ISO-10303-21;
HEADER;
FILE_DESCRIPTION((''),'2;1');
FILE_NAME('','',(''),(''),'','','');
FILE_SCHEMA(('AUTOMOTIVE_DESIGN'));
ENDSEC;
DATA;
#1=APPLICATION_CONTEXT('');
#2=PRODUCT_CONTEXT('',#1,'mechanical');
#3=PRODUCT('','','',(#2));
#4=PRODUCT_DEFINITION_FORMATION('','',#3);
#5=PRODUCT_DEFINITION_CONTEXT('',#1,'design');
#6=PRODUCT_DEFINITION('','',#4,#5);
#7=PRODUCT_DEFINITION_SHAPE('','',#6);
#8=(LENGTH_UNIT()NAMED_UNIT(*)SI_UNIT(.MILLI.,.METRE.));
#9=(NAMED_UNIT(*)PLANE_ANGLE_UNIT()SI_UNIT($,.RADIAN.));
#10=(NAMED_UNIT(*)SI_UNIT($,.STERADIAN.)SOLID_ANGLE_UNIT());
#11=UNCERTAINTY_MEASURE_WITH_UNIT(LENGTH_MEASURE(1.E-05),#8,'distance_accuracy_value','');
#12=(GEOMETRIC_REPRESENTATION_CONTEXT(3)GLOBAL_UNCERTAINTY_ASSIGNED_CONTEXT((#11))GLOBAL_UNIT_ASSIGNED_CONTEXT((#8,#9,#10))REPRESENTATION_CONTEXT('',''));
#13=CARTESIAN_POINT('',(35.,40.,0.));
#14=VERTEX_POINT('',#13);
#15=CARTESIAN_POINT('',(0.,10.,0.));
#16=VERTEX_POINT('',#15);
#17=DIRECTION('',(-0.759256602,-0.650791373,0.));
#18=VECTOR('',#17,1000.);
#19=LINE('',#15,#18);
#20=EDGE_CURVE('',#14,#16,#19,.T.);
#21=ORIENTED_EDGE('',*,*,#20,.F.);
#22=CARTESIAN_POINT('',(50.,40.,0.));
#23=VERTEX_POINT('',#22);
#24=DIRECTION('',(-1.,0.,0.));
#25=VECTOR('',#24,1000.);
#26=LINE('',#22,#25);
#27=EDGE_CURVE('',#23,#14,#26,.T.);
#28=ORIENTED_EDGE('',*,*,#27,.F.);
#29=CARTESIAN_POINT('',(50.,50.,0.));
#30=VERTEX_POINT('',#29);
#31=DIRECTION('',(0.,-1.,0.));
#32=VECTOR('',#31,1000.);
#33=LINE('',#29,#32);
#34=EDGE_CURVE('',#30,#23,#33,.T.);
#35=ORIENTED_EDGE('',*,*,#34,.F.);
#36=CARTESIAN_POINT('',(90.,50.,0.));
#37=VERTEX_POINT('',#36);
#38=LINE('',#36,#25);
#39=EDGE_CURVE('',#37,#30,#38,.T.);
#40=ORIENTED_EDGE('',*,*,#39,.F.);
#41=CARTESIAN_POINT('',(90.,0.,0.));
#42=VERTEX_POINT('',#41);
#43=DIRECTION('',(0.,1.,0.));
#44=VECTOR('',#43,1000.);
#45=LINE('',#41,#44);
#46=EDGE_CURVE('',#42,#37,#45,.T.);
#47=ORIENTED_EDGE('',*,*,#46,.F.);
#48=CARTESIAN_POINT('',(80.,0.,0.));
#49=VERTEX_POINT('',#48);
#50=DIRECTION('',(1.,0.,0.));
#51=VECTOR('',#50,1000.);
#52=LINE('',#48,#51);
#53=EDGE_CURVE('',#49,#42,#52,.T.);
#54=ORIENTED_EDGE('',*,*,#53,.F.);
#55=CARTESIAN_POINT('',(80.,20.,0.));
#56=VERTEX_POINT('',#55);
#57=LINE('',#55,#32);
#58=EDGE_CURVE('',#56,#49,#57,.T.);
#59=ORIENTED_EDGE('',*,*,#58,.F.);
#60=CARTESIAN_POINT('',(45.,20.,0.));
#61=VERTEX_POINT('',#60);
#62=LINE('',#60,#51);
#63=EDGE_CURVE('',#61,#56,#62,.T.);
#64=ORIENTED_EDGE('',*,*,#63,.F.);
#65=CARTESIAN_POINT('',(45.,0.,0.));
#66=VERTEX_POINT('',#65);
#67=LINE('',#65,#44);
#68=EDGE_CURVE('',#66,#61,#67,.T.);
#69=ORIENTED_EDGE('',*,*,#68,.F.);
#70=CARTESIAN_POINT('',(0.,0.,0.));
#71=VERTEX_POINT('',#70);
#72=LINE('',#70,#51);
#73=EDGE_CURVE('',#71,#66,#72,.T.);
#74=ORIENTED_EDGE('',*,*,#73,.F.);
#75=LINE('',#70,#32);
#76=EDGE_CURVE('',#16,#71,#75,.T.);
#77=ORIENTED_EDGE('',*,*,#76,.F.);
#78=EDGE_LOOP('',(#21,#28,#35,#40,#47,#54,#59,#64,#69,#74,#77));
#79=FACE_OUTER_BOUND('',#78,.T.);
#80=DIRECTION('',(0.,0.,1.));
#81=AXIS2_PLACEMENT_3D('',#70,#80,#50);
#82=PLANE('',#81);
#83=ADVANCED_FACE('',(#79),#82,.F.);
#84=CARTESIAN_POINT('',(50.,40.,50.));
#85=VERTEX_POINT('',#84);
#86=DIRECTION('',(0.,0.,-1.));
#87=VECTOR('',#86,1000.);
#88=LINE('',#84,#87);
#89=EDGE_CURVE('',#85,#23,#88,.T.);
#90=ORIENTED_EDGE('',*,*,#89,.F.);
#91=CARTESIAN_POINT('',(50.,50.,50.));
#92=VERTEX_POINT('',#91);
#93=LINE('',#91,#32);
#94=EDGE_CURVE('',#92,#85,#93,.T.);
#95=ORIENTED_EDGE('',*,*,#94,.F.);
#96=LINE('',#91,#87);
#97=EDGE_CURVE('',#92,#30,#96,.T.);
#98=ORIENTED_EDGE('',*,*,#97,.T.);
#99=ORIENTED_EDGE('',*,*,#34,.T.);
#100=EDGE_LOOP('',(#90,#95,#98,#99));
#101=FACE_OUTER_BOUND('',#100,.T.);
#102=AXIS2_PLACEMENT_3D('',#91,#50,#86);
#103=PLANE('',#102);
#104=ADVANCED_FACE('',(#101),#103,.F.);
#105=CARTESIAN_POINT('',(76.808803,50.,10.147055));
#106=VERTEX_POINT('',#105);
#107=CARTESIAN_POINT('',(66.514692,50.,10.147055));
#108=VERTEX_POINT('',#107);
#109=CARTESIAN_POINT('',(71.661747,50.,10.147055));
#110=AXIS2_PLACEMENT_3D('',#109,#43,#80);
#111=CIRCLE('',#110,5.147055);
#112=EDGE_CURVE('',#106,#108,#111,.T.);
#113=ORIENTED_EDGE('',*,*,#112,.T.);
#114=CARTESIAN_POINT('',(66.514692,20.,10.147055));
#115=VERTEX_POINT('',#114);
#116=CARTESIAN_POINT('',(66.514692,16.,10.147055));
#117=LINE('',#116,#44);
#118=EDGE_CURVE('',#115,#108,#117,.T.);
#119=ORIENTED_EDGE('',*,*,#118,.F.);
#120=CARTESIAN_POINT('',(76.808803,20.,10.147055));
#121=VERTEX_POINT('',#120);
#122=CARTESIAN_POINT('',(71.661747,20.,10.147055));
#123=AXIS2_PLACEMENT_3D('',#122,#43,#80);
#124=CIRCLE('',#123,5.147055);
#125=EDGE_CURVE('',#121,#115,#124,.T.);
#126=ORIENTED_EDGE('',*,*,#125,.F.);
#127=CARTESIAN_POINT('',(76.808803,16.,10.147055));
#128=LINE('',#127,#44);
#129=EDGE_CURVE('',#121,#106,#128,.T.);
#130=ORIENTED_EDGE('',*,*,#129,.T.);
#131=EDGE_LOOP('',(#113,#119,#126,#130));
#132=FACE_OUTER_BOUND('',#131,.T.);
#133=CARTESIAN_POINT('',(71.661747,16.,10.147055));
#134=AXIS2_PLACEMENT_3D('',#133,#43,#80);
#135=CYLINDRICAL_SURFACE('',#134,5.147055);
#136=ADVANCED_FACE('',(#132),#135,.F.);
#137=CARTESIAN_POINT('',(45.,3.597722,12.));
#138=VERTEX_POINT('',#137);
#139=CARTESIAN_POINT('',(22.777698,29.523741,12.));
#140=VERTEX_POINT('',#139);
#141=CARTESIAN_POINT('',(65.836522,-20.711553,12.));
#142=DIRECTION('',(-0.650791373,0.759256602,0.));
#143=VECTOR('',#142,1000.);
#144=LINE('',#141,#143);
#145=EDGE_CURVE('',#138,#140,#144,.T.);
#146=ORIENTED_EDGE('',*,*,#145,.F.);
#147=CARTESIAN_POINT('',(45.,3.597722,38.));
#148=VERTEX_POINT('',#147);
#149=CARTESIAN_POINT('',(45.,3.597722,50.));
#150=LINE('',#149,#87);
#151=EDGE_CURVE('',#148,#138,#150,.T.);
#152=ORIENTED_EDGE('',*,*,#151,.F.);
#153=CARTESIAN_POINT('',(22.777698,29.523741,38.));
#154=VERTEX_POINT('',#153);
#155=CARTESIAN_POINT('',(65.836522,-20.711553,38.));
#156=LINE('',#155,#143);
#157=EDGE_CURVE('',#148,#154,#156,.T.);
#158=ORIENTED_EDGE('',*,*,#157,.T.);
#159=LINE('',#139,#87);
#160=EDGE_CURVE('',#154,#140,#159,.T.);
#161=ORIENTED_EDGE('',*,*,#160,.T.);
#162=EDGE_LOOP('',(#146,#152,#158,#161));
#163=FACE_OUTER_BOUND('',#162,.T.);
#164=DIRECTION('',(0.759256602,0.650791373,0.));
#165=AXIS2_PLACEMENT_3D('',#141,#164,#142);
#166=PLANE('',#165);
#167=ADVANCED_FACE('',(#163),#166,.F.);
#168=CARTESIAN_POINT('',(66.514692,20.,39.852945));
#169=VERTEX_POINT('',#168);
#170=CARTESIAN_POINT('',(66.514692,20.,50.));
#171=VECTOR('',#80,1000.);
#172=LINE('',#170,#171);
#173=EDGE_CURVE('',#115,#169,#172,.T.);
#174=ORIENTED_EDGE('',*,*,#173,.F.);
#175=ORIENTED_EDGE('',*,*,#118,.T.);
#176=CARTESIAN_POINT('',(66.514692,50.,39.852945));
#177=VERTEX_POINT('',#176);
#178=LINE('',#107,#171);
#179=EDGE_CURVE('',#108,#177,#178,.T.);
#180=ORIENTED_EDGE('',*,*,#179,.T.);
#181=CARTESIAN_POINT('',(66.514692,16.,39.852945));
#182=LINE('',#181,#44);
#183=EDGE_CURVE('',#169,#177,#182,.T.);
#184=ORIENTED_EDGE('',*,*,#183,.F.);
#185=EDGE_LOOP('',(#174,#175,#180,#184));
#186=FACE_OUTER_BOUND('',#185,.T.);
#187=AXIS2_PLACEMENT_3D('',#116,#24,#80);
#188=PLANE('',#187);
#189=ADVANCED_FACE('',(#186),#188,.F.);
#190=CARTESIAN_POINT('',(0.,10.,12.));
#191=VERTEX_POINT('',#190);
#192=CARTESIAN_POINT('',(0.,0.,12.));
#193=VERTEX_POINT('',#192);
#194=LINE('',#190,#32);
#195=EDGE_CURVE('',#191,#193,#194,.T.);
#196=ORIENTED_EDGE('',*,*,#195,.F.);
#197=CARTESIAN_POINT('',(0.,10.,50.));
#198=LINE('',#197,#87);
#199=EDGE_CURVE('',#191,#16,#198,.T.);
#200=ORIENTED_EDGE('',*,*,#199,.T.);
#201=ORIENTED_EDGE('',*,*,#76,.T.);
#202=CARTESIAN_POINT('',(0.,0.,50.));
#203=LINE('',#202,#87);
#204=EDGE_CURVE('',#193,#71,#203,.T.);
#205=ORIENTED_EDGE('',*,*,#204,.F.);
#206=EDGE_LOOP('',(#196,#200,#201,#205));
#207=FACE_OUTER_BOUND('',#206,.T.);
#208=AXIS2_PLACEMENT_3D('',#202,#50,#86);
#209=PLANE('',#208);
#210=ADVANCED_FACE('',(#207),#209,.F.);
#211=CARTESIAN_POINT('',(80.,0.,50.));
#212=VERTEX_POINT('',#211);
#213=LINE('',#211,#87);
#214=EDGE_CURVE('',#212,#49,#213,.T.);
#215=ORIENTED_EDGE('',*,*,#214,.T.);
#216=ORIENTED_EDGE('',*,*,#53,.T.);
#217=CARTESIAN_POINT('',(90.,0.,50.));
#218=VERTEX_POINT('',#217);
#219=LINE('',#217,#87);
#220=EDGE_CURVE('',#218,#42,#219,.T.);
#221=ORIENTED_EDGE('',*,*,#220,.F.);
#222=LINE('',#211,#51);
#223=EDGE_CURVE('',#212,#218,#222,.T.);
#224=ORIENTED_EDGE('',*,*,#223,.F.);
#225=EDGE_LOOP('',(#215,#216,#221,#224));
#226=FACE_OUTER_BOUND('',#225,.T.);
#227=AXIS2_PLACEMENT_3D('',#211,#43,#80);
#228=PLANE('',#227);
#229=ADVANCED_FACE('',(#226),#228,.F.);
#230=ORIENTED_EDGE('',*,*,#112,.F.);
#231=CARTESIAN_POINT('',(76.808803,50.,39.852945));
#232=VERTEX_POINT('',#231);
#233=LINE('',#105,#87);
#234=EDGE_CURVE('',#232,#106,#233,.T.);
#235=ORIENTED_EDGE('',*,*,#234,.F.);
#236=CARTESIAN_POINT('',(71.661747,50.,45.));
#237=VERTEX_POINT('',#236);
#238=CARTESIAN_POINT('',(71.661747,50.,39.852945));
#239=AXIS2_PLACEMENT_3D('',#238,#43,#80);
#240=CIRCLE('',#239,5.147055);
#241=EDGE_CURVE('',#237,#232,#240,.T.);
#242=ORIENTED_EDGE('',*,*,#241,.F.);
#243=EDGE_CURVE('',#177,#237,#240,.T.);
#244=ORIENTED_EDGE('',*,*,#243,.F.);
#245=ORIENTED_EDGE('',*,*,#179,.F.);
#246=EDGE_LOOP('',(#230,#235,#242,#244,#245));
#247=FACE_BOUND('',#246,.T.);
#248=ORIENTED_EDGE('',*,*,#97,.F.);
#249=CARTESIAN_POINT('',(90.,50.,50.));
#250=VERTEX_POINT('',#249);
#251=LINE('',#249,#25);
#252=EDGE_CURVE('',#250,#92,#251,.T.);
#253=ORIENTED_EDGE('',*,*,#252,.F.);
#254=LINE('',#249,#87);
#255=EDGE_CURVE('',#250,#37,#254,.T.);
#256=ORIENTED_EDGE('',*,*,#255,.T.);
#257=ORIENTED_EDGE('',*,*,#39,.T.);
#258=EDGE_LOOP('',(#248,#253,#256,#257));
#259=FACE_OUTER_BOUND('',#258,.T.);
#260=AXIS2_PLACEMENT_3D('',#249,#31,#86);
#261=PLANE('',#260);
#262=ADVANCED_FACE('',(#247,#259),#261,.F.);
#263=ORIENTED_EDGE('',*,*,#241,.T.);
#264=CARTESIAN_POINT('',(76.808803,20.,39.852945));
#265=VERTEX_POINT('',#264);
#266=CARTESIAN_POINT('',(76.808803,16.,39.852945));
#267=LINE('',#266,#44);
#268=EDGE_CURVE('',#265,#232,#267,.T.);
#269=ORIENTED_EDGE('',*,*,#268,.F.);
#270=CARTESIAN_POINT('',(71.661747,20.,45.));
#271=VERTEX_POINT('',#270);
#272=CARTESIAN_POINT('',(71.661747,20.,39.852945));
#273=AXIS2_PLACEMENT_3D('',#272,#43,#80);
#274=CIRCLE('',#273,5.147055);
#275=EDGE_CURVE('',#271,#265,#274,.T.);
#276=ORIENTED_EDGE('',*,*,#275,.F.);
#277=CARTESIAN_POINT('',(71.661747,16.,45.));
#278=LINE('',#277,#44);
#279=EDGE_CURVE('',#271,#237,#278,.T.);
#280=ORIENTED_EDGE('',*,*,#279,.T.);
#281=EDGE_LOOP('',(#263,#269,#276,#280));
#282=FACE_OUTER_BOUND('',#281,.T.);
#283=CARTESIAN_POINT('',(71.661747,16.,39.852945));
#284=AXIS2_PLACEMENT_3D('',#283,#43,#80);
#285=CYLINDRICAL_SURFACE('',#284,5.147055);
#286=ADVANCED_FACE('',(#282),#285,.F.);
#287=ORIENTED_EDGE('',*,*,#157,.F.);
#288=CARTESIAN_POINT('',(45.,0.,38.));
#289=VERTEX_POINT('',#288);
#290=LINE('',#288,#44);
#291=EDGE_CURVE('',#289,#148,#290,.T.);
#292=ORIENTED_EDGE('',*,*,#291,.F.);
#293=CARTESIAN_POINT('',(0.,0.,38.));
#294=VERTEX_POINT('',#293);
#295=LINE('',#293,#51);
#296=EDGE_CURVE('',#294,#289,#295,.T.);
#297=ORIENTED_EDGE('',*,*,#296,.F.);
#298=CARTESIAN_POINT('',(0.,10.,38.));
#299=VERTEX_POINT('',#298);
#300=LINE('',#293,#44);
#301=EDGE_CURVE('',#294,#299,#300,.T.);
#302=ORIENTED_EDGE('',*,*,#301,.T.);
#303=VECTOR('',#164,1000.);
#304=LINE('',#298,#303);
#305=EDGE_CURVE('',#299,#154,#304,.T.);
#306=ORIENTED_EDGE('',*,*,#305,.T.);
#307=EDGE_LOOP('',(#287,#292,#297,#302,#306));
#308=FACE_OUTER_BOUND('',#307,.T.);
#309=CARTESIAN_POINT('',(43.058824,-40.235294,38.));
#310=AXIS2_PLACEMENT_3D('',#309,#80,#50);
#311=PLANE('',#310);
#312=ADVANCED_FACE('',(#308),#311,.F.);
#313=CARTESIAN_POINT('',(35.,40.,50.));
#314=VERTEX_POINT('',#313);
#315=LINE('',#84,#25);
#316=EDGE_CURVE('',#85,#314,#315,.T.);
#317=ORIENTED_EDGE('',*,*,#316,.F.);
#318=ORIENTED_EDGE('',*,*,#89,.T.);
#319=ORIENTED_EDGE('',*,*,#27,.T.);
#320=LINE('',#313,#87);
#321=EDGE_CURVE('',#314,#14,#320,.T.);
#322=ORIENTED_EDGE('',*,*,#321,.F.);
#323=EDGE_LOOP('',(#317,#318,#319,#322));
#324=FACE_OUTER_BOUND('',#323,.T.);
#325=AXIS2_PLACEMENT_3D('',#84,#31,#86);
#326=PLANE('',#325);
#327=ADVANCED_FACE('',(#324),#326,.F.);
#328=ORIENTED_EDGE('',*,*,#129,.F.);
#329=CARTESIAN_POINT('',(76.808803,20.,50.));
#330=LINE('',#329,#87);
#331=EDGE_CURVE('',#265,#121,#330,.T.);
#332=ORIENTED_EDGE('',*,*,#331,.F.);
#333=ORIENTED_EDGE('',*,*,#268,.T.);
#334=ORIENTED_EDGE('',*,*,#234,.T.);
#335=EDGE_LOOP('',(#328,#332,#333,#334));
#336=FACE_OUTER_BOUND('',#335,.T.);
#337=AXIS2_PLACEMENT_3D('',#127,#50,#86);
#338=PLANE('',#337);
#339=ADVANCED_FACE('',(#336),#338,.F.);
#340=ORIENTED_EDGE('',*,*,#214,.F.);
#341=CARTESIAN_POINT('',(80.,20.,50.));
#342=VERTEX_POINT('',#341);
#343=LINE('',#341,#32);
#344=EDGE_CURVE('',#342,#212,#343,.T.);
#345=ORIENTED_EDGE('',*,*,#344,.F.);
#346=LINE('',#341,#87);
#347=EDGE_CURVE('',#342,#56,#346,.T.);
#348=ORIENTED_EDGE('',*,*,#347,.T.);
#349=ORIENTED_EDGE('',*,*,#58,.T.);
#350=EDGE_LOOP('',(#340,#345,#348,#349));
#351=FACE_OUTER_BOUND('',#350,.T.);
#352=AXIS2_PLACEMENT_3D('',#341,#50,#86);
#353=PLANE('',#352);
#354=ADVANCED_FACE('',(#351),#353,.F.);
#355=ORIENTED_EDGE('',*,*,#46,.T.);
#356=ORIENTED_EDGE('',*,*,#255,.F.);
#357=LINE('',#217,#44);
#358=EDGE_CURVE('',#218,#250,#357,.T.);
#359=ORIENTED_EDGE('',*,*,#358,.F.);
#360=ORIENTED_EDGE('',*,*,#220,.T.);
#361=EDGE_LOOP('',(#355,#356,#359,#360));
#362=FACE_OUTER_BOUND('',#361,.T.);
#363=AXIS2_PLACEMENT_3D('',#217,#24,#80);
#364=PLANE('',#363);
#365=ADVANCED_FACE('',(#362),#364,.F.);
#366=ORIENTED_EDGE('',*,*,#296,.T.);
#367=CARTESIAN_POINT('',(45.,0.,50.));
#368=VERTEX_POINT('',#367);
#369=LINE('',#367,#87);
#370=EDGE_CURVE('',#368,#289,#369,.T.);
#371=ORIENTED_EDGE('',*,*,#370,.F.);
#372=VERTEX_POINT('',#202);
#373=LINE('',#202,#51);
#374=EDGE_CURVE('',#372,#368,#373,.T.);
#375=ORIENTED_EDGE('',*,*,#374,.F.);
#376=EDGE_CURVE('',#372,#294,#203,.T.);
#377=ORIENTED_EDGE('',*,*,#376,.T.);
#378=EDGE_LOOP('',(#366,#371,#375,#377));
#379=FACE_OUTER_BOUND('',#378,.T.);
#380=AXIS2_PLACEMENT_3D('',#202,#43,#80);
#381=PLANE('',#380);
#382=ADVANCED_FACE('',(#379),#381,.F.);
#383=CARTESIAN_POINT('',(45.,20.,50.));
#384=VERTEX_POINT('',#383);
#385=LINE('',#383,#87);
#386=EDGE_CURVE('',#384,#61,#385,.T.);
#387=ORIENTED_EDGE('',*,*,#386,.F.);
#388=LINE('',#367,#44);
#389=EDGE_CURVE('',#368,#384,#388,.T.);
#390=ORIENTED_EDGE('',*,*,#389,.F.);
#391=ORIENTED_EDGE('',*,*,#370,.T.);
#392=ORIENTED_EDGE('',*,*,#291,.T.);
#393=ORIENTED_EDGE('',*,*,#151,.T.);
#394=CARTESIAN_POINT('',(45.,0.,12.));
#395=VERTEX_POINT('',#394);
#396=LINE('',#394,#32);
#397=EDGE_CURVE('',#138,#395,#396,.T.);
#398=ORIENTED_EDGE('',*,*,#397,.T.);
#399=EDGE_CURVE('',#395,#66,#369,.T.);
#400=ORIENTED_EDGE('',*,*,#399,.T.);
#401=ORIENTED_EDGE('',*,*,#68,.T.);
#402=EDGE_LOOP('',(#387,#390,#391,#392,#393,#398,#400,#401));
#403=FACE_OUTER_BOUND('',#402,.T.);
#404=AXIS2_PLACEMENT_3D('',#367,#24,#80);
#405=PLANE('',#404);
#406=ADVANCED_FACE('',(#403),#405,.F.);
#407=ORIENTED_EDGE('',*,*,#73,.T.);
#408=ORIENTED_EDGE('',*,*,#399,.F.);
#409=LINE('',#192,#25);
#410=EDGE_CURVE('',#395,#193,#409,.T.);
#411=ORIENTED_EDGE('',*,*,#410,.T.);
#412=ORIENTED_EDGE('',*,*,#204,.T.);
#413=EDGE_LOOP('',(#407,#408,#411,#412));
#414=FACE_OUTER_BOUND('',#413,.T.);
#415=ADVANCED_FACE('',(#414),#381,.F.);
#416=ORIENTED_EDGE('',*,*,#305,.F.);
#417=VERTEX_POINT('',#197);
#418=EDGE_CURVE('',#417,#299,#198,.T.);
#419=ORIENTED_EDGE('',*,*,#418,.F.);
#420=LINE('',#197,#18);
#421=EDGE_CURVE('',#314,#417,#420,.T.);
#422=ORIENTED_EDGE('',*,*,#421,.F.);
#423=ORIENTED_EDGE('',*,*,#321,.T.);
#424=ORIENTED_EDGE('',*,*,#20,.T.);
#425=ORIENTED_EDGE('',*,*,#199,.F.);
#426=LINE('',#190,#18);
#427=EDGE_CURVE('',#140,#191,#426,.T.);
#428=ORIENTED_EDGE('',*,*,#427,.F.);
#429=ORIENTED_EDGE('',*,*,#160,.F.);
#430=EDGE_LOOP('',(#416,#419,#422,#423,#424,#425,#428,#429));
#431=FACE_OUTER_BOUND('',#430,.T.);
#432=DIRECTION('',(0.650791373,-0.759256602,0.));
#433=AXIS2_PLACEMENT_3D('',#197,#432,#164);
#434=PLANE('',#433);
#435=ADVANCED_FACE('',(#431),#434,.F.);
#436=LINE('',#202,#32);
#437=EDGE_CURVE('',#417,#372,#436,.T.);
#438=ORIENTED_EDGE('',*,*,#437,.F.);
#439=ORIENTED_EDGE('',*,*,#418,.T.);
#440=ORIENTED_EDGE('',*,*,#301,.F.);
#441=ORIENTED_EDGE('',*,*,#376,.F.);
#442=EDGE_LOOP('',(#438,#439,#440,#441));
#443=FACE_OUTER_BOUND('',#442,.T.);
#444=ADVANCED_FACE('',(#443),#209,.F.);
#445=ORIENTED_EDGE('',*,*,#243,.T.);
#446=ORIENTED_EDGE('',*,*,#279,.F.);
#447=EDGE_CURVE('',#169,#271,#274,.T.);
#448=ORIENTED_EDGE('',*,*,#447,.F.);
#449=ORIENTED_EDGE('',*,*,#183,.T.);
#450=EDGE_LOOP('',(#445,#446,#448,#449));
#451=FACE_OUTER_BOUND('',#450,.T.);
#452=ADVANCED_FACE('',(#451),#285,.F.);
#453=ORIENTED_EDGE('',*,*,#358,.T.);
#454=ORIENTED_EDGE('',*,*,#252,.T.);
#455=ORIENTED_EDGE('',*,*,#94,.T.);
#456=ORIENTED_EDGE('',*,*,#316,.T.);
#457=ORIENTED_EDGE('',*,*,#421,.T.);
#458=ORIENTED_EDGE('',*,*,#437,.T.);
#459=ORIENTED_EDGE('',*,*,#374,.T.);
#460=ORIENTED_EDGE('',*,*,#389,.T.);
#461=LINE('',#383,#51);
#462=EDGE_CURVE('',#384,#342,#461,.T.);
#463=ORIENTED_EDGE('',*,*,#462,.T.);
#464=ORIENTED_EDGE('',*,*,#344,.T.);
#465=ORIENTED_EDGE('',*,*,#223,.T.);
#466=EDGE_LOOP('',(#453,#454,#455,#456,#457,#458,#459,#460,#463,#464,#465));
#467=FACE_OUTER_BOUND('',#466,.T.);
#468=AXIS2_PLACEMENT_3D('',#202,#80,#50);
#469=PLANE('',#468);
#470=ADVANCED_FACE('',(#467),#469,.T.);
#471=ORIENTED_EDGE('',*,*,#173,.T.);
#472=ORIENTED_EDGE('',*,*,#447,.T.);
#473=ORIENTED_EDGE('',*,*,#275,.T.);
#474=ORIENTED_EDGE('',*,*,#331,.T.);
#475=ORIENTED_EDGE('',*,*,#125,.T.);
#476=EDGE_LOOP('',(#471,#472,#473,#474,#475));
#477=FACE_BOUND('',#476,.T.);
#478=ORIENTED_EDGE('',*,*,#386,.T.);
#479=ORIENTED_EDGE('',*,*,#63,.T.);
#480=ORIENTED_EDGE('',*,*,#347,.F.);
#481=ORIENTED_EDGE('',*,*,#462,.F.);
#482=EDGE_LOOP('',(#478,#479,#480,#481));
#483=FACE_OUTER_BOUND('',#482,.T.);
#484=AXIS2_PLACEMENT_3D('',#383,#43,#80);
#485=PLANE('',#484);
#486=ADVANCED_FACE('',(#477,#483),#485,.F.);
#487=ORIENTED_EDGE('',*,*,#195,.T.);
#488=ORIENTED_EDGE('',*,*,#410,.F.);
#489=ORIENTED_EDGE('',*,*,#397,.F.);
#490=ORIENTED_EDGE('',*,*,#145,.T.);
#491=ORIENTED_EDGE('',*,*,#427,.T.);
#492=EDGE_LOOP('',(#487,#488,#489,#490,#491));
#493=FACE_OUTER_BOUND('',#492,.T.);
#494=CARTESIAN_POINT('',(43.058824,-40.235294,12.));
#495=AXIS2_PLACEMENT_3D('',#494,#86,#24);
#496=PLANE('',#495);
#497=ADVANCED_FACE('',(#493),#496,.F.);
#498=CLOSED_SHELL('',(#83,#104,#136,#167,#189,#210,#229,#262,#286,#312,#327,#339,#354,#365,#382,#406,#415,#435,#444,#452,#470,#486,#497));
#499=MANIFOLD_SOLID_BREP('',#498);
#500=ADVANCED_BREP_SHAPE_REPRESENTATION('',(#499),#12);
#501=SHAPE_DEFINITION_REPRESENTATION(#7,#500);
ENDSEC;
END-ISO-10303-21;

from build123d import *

# Parameters (mm, degrees)
SUPPORT_BODY_50MM_DEPTH    = 50
TOP_SLOT_34MM_DEEP_DEPTH   = 34
CLEVIS_NOTCH_SKETCH_W      = 30
CLEVIS_NOTCH_SKETCH_H      = 26
CLEVIS_NOTCH_DEPTH         = 117.062863291
SIDE_RELIEF_SKETCH_W       = 26
SIDE_RELIEF_SKETCH_H       = 10
SIDE_RELIEF_CUT_10MM_DEPTH = 10


with BuildPart() as part:
    # Support Profile Sketch → Support Body 50mm (new body)
    with BuildSketch(Plane.XY):
        Polygon((0, 0), (45, 0), (45, 20), (80, 20), (80, 0), (90, 0), (90, 50), (50, 50), (50, 40), (35, 40), (0, 10), align=None)
    extrude(amount=SUPPORT_BODY_50MM_DEPTH)

    # Top Slot Sketch → Top Slot 34mm Deep (cut)
    with BuildSketch(Plane(origin=(0, 50, 0), x_dir=(1, 0, 0), z_dir=(0, 1, 0))):
        with BuildLine():
            Line((76.808802697, -10.147055453), (76.808802697, -39.852944547))
            ThreePointArc((76.808802697, -39.852944547), (71.661747244, -45), (66.514691792, -39.852944547))
            Line((66.514691792, -39.852944547), (66.514691792, -10.147055453))
            ThreePointArc((66.514691792, -10.147055453), (71.661747244, -5), (76.808802697, -10.147055453))
        make_face()
    extrude(amount=-TOP_SLOT_34MM_DEEP_DEPTH, mode=Mode.SUBTRACT)

    # Clevis Notch Sketch → Clevis Notch (cut, through all)
    with BuildSketch(Plane(origin=(-4.941176471, 5.764705882, 0), x_dir=(0.7592566023652966, 0.6507913734559686, 0), z_dir=(-0.6507913734559686, 0.7592566023652966, 0))):
        with Locations((21.507913735, -25)):
            Rectangle(CLEVIS_NOTCH_SKETCH_W, CLEVIS_NOTCH_SKETCH_H)
    extrude(amount=-CLEVIS_NOTCH_DEPTH, mode=Mode.SUBTRACT)

    # Side Relief Sketch → Side Relief Cut 10mm (cut)
    with BuildSketch(Plane.ZY):
        with Locations((25, 5)):
            Rectangle(SIDE_RELIEF_SKETCH_W, SIDE_RELIEF_SKETCH_H)
    extrude(amount=-SIDE_RELIEF_CUT_10MM_DEPTH, mode=Mode.SUBTRACT)


solid = part.part
